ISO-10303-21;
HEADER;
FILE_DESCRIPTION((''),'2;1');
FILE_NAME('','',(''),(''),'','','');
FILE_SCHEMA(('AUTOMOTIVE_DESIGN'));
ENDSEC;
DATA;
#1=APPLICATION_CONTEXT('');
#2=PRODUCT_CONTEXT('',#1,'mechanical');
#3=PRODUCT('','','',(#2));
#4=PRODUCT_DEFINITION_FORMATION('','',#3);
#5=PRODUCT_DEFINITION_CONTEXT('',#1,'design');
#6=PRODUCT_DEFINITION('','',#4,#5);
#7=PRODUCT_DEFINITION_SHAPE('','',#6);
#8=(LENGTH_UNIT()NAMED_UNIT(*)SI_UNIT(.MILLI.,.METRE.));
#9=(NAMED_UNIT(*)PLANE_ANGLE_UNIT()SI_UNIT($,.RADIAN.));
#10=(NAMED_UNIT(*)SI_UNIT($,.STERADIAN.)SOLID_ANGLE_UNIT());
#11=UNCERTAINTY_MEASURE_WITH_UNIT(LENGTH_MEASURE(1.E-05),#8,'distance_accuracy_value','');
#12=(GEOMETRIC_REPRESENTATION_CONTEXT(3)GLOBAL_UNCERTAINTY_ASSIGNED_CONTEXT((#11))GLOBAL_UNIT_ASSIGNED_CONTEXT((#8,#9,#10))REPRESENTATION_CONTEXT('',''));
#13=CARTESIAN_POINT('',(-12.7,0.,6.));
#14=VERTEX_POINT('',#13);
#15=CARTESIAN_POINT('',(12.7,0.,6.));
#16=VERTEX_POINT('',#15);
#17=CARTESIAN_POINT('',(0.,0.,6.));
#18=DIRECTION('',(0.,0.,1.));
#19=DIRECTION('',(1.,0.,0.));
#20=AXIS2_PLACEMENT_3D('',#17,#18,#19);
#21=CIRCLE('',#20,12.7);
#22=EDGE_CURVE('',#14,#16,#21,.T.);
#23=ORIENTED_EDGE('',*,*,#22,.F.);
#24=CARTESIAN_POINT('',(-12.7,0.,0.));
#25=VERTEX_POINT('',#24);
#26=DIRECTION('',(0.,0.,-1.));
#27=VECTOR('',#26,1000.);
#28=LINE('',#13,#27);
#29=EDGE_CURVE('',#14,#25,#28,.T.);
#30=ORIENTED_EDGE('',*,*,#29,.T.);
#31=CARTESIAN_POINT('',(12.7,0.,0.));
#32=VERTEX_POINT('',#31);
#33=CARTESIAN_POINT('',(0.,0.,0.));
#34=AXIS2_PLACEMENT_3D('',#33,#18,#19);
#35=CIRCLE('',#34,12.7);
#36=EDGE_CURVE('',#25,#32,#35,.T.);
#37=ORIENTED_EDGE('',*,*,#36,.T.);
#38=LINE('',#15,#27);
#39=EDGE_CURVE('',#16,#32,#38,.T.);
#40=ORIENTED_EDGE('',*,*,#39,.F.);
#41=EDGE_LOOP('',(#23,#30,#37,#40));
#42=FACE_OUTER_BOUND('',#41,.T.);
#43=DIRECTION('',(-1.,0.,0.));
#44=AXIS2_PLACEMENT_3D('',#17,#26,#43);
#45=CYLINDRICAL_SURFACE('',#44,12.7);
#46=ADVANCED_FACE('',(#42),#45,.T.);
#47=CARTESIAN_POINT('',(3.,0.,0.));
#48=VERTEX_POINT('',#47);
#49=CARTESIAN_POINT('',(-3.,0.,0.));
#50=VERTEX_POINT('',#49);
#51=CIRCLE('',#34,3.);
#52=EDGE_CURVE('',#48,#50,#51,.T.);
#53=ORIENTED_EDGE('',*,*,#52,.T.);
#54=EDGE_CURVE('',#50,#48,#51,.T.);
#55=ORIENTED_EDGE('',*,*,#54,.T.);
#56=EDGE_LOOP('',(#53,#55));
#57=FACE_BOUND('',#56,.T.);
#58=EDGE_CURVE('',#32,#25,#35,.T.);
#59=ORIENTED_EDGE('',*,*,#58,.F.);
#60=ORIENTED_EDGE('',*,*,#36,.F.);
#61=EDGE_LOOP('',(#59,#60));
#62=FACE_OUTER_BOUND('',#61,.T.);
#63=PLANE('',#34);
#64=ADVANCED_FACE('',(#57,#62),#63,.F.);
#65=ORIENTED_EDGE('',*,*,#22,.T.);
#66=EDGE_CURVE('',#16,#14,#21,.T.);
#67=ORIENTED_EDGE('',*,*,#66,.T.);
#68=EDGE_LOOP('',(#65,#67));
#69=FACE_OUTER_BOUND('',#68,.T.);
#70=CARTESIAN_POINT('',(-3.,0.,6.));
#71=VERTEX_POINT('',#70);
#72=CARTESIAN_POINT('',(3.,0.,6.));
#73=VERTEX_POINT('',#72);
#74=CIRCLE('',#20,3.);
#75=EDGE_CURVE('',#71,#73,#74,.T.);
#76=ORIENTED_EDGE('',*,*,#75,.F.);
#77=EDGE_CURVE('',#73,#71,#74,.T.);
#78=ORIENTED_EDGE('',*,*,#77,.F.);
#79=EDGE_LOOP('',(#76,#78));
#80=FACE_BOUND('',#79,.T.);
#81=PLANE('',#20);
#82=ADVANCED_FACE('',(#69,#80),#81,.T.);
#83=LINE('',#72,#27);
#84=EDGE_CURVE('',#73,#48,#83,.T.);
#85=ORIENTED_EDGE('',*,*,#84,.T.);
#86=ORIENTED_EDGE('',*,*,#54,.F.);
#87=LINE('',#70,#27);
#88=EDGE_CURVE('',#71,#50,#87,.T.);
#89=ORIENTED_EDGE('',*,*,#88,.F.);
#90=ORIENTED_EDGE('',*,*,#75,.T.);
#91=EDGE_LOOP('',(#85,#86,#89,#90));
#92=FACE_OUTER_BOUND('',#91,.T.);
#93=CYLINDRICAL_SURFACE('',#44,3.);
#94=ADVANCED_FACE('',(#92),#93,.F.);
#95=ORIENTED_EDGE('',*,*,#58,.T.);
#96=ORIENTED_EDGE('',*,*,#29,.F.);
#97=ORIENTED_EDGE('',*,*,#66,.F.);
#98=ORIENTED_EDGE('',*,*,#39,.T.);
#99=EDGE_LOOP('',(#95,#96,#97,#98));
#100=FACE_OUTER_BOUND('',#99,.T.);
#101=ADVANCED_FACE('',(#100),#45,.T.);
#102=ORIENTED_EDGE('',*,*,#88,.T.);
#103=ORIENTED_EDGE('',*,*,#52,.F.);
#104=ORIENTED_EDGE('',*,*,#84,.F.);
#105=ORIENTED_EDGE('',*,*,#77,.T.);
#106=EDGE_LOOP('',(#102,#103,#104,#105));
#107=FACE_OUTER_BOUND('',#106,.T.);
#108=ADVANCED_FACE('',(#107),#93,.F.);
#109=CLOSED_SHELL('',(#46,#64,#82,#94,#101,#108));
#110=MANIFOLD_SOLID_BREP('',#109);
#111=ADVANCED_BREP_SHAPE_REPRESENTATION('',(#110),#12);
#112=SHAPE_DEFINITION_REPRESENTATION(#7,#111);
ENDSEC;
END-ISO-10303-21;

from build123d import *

# Parameters (mm, degrees)
SKETCH1_R           = 12.7
SKETCH1_R_2         = 3
BOSS_EXTRUDE1_DEPTH = 6


with BuildPart() as part:
    # Sketch1 → Boss-Extrude1 (new body)
    with BuildSketch(Plane.XY):
        Circle(SKETCH1_R)
        Circle(SKETCH1_R_2, mode=Mode.SUBTRACT)
    extrude(amount=BOSS_EXTRUDE1_DEPTH)


solid = part.part
